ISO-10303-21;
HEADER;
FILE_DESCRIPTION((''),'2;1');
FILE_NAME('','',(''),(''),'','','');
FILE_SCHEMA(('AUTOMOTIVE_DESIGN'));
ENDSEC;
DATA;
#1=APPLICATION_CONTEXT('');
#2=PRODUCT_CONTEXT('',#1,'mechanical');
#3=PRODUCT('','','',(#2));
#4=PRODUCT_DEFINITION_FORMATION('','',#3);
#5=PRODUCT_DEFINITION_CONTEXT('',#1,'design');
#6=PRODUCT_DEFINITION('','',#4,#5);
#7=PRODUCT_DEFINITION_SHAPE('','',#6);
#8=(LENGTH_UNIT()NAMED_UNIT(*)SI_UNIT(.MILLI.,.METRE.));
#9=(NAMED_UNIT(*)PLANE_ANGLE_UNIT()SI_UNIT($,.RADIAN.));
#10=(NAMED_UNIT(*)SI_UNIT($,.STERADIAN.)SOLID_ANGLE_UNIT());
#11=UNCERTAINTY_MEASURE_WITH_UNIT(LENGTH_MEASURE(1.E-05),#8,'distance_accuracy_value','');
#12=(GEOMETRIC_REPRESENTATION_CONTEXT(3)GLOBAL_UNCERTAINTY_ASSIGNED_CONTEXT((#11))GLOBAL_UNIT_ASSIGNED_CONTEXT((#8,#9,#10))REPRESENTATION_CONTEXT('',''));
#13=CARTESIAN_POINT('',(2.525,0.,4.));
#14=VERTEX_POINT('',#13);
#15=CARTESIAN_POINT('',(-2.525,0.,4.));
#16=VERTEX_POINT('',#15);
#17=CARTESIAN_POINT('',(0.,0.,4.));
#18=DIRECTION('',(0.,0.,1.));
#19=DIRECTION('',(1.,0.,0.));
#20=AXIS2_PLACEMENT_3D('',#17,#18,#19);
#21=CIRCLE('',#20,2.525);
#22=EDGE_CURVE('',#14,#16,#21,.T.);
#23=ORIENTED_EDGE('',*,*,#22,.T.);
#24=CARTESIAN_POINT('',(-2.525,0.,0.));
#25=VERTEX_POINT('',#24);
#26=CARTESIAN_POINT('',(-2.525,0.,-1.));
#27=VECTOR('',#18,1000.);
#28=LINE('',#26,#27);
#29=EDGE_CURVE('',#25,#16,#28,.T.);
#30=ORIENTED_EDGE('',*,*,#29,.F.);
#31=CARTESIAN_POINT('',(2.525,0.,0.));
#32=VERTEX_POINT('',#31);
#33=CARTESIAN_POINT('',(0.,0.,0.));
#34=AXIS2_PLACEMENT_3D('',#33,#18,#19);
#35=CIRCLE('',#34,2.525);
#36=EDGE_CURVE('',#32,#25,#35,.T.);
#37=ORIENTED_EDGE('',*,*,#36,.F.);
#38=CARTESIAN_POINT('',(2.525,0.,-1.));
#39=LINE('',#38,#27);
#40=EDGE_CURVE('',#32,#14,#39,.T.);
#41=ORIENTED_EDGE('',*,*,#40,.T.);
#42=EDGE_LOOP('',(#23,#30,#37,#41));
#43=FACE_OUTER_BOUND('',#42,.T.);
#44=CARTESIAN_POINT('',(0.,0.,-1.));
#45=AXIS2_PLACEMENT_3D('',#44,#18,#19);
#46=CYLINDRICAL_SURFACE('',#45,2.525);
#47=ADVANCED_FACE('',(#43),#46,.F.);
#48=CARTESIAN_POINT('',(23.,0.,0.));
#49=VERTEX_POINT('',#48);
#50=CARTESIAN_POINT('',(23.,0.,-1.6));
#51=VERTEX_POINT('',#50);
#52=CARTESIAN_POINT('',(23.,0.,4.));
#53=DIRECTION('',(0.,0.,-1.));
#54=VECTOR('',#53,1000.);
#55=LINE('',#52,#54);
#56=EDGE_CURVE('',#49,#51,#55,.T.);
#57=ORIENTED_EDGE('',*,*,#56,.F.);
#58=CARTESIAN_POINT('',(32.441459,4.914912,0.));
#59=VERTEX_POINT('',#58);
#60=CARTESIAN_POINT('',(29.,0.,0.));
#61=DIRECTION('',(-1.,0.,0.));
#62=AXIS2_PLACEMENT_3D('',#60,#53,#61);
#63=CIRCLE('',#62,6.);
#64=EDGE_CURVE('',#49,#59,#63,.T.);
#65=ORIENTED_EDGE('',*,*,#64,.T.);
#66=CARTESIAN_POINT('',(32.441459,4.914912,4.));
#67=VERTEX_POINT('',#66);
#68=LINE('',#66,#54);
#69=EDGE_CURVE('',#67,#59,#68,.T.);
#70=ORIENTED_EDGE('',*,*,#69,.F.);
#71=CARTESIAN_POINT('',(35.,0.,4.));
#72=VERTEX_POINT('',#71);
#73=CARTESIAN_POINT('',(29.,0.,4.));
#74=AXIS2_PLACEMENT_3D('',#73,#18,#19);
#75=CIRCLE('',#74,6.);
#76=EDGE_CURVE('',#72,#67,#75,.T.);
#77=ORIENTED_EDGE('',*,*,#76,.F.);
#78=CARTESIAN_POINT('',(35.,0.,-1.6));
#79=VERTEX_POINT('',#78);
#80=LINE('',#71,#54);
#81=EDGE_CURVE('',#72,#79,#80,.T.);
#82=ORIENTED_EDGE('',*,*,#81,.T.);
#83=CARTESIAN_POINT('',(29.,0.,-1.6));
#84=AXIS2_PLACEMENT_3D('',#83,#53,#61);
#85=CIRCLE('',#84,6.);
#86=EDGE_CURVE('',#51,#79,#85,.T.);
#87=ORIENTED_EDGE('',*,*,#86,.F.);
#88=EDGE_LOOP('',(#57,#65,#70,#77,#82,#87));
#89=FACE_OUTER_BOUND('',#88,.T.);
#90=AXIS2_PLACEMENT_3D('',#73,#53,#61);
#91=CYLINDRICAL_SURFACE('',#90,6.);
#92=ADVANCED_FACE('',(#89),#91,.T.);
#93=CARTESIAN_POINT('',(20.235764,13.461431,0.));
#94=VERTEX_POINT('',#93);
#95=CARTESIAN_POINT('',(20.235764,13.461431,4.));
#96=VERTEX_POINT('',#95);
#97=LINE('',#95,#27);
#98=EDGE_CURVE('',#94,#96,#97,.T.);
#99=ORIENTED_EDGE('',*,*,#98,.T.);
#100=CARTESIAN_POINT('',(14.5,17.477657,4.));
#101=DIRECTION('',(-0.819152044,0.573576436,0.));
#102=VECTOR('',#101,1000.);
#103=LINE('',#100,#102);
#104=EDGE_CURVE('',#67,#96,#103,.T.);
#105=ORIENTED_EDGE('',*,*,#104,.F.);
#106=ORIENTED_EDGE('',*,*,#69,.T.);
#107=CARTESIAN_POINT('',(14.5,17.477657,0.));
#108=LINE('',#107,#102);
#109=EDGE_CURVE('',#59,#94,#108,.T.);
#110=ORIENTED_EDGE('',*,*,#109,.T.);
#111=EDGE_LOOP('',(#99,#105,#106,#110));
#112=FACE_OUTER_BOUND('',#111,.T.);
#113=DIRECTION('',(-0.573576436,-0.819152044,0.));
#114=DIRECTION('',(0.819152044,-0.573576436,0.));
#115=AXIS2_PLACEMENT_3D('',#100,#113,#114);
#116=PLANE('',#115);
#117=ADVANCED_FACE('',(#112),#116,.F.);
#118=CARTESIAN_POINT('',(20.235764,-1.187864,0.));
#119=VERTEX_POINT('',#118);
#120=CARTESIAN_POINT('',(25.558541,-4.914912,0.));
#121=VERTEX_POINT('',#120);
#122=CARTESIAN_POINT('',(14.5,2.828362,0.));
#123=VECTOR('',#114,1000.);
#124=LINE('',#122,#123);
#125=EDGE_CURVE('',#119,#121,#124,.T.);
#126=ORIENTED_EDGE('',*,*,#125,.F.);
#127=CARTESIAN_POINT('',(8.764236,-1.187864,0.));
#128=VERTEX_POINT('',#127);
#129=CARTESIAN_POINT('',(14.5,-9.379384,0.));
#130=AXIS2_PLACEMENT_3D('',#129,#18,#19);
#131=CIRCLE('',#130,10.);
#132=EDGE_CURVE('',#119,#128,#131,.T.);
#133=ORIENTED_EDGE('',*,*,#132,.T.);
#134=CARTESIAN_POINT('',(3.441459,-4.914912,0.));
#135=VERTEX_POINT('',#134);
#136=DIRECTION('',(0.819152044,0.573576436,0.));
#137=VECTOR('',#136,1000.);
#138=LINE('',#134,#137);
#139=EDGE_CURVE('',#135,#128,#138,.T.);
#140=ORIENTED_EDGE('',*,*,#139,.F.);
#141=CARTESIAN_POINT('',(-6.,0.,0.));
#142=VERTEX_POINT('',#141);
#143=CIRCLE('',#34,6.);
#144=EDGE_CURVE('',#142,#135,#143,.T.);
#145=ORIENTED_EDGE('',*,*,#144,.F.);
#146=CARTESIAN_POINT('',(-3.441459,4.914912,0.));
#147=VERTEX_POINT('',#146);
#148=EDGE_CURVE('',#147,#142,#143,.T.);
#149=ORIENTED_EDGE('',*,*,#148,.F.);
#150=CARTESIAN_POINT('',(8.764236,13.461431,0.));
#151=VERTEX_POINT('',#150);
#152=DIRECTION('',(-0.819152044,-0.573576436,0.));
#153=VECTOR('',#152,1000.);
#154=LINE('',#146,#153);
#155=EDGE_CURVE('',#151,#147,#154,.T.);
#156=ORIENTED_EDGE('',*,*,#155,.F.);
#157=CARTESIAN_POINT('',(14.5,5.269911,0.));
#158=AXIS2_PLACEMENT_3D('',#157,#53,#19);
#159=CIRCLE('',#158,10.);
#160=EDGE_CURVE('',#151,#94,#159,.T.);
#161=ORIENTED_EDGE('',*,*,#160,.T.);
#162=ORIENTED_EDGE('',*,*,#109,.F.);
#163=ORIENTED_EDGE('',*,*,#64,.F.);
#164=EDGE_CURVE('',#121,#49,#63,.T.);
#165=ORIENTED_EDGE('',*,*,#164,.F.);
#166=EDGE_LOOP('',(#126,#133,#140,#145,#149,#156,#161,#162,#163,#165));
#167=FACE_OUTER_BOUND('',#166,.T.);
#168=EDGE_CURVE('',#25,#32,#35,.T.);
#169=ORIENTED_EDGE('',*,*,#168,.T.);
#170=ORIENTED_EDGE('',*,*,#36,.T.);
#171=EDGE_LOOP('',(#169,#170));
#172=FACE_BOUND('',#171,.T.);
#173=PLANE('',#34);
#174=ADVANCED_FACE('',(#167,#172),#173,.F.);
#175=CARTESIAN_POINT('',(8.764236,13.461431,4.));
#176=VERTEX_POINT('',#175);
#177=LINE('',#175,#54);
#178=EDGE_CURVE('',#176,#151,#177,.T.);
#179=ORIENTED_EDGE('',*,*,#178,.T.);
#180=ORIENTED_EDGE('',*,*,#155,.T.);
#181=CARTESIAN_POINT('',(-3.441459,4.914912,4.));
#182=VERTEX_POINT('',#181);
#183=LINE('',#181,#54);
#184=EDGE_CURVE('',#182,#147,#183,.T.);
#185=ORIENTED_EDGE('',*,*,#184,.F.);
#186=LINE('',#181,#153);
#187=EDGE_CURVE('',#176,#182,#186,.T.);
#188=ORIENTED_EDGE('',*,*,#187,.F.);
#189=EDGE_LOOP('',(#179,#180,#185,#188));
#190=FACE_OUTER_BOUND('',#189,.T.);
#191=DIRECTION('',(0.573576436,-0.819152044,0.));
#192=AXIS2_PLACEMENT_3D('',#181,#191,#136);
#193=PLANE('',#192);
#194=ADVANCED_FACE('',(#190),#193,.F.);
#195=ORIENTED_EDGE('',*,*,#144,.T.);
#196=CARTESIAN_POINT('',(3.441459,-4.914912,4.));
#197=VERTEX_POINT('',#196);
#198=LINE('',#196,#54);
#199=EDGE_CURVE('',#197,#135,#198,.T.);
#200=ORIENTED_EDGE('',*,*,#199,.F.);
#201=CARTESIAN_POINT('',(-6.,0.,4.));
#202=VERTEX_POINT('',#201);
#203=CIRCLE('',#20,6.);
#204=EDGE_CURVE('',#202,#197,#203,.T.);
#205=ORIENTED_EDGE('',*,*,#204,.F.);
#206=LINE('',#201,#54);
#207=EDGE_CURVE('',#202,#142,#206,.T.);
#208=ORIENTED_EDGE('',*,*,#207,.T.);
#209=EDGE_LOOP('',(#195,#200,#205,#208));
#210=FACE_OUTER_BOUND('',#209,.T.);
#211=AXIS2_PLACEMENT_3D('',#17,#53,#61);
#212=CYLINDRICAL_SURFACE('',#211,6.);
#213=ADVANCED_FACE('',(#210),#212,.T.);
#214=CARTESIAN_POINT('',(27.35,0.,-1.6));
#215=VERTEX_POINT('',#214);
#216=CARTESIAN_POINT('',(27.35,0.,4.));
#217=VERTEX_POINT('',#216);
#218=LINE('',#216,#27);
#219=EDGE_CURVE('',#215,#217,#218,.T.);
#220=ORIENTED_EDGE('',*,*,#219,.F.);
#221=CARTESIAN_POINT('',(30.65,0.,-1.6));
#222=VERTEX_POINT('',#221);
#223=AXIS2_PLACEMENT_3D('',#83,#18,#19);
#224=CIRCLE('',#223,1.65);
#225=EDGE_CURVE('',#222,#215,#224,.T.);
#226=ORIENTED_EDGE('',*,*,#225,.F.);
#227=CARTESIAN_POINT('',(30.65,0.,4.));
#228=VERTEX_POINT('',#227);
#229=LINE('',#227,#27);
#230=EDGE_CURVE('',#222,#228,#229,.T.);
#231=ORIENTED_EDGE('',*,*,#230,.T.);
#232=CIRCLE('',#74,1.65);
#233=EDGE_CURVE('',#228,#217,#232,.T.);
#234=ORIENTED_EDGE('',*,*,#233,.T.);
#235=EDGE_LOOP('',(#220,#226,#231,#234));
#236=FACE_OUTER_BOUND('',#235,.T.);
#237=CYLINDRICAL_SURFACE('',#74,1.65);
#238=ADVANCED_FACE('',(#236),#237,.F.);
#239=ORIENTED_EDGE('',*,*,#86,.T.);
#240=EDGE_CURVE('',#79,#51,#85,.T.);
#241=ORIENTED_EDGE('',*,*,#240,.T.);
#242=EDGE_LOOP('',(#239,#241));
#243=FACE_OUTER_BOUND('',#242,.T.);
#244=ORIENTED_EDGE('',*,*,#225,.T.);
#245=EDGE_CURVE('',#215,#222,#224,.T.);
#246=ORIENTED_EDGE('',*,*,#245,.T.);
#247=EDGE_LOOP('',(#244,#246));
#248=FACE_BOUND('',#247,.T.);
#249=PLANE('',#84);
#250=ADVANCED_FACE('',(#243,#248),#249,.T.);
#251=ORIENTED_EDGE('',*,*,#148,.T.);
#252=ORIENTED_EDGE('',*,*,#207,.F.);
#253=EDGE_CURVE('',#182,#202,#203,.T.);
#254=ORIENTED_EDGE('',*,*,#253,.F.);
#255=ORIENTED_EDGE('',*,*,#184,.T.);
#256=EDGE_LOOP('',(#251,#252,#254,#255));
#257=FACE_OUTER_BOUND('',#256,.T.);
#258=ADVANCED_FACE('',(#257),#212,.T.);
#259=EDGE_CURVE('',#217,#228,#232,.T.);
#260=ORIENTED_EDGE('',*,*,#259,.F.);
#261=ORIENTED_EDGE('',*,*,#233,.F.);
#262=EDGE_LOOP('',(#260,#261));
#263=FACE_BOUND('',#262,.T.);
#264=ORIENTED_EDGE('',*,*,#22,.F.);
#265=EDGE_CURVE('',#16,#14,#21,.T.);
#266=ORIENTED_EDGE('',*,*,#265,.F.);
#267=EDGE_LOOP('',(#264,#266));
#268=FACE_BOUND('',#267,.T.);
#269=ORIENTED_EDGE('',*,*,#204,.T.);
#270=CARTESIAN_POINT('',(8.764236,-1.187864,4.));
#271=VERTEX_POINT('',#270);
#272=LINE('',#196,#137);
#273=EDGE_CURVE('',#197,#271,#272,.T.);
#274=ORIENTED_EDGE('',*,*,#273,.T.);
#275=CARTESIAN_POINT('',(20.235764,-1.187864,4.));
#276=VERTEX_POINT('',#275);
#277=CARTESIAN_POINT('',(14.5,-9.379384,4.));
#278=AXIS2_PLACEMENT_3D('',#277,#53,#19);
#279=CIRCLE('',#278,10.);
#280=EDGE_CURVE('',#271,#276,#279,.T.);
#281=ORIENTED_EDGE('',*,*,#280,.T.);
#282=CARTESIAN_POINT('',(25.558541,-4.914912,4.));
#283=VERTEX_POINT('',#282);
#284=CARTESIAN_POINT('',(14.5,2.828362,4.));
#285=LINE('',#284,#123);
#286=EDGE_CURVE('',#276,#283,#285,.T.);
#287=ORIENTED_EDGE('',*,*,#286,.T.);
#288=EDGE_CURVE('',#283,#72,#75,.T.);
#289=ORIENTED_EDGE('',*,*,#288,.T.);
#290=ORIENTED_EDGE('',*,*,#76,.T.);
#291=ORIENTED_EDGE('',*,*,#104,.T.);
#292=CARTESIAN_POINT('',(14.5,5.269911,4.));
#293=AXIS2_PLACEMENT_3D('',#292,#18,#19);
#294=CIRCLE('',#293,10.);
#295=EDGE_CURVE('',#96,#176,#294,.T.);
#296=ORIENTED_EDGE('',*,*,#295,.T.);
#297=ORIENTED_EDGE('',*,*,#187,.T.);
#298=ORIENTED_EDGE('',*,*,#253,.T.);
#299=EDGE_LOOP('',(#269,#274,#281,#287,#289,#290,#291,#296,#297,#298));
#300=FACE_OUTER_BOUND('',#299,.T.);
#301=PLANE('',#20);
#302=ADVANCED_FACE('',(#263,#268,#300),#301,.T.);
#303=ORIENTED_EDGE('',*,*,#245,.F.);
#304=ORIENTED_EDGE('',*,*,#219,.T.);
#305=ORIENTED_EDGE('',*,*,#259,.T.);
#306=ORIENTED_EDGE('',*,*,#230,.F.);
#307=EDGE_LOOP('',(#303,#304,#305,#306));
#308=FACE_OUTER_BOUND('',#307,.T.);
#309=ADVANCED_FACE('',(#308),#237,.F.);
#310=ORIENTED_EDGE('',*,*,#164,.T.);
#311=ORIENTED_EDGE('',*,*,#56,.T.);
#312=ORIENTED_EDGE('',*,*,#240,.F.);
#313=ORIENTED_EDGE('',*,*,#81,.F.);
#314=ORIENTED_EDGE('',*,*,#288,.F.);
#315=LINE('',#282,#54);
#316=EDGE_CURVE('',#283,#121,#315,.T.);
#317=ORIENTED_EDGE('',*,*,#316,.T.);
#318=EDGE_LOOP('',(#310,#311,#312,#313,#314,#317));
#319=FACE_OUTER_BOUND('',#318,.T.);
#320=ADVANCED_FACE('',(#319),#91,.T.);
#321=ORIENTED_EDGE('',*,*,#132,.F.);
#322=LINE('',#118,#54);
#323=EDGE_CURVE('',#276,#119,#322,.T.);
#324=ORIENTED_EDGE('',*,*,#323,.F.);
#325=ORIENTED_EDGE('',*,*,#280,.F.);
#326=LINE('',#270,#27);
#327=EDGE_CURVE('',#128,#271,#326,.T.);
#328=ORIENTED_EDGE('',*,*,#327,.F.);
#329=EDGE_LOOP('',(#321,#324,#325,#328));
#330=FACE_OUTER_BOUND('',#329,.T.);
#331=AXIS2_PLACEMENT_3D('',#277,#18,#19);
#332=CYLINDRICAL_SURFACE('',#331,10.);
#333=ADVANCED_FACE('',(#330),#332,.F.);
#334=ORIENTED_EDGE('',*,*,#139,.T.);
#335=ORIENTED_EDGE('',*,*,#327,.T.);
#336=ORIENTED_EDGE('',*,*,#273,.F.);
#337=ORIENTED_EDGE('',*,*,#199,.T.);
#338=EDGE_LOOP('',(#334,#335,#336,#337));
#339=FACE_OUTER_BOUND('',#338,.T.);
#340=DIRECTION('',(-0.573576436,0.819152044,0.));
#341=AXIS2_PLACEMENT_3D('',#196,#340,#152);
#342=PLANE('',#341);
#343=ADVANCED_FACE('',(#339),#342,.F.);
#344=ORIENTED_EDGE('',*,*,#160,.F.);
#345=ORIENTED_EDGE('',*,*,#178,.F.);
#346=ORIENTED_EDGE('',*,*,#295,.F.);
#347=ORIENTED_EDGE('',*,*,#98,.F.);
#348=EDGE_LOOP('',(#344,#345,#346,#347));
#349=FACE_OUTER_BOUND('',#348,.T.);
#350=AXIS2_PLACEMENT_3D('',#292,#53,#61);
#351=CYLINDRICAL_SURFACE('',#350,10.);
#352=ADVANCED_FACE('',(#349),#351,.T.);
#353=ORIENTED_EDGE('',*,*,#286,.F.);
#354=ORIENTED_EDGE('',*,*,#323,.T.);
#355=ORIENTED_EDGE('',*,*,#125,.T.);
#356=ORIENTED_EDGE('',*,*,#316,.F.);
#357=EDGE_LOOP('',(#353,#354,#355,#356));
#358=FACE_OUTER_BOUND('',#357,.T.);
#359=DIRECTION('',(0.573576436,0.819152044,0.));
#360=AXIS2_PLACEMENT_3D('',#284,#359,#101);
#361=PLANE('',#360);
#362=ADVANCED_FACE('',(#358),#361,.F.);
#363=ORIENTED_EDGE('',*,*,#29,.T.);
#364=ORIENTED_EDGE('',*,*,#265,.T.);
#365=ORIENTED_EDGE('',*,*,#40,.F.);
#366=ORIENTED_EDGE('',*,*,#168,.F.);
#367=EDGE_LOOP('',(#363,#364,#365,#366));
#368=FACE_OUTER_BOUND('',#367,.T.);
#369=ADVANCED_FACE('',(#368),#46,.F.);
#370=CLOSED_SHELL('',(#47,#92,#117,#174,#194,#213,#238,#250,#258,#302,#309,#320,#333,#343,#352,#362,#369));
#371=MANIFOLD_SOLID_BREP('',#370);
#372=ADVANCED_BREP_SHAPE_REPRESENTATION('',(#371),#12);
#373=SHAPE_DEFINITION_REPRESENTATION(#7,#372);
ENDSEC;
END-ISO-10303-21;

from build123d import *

# Parameters (mm, degrees)
BOSS_EXTRUDE1_DEPTH = 4
SKETCH2_R           = 2.525
CUT_EXTRUDE1_DEPTH  = 5
BOSS_EXTRUDE2_START = 1.6
SKETCH7_R           = 6
BOSS_EXTRUDE2_DEPTH = 1.6
M4_TAPPED_HOLE1_D   = 3.3
FILLET1_R           = 10


with BuildPart() as part:
    # Sketch1 → Boss-Extrude1 (new body)
    with BuildSketch(Plane.XY):
        with BuildLine():
            Line((3.441458618, -4.914912266), (14.5, 2.828361771))
            Line((14.5, 2.828361771), (25.558541382, -4.914912266))
            ThreePointArc((25.558541382, -4.914912266), (33.914912266, -3.441458618), (32.441458618, 4.914912266))
            Line((32.441458618, 4.914912266), (14.5, 17.477656837))
            Line((14.5, 17.477656837), (-3.441458618, 4.914912266))
            ThreePointArc((-3.441458618, 4.914912266), (-4.914912266, -3.441458618), (3.441458618, -4.914912266))
        make_face()
    extrude(amount=BOSS_EXTRUDE1_DEPTH)

    # Sketch2 → Cut-Extrude1 (cut)
    with BuildSketch(Plane.XY.offset(4)):
        Circle(SKETCH2_R)
    extrude(amount=-CUT_EXTRUDE1_DEPTH, mode=Mode.SUBTRACT)

    # Sketch7 → Boss-Extrude2 (add)
    with BuildSketch(Plane(origin=(0, 0, 0), x_dir=(-1, 0, 0), z_dir=(0, 0, -1)).offset(BOSS_EXTRUDE2_START)):
        with Locations((-29, 0)):
            Circle(SKETCH7_R)
    extrude(amount=-BOSS_EXTRUDE2_DEPTH)

    # M4 Tapped Hole1 (through all)
    with Locations(Plane.XY.offset(4)):
        with Locations((29, 0)):
            Hole(M4_TAPPED_HOLE1_D / 2)

    # Fillet1
    fillet1_edges = [part.edges().sort_by_distance(p)[0] for p in [
        (14.5, 17.477656837, 2),
        (14.5, 2.828361771, 2),
    ]]
    fillet(fillet1_edges, radius=FILLET1_R)


solid = part.part
